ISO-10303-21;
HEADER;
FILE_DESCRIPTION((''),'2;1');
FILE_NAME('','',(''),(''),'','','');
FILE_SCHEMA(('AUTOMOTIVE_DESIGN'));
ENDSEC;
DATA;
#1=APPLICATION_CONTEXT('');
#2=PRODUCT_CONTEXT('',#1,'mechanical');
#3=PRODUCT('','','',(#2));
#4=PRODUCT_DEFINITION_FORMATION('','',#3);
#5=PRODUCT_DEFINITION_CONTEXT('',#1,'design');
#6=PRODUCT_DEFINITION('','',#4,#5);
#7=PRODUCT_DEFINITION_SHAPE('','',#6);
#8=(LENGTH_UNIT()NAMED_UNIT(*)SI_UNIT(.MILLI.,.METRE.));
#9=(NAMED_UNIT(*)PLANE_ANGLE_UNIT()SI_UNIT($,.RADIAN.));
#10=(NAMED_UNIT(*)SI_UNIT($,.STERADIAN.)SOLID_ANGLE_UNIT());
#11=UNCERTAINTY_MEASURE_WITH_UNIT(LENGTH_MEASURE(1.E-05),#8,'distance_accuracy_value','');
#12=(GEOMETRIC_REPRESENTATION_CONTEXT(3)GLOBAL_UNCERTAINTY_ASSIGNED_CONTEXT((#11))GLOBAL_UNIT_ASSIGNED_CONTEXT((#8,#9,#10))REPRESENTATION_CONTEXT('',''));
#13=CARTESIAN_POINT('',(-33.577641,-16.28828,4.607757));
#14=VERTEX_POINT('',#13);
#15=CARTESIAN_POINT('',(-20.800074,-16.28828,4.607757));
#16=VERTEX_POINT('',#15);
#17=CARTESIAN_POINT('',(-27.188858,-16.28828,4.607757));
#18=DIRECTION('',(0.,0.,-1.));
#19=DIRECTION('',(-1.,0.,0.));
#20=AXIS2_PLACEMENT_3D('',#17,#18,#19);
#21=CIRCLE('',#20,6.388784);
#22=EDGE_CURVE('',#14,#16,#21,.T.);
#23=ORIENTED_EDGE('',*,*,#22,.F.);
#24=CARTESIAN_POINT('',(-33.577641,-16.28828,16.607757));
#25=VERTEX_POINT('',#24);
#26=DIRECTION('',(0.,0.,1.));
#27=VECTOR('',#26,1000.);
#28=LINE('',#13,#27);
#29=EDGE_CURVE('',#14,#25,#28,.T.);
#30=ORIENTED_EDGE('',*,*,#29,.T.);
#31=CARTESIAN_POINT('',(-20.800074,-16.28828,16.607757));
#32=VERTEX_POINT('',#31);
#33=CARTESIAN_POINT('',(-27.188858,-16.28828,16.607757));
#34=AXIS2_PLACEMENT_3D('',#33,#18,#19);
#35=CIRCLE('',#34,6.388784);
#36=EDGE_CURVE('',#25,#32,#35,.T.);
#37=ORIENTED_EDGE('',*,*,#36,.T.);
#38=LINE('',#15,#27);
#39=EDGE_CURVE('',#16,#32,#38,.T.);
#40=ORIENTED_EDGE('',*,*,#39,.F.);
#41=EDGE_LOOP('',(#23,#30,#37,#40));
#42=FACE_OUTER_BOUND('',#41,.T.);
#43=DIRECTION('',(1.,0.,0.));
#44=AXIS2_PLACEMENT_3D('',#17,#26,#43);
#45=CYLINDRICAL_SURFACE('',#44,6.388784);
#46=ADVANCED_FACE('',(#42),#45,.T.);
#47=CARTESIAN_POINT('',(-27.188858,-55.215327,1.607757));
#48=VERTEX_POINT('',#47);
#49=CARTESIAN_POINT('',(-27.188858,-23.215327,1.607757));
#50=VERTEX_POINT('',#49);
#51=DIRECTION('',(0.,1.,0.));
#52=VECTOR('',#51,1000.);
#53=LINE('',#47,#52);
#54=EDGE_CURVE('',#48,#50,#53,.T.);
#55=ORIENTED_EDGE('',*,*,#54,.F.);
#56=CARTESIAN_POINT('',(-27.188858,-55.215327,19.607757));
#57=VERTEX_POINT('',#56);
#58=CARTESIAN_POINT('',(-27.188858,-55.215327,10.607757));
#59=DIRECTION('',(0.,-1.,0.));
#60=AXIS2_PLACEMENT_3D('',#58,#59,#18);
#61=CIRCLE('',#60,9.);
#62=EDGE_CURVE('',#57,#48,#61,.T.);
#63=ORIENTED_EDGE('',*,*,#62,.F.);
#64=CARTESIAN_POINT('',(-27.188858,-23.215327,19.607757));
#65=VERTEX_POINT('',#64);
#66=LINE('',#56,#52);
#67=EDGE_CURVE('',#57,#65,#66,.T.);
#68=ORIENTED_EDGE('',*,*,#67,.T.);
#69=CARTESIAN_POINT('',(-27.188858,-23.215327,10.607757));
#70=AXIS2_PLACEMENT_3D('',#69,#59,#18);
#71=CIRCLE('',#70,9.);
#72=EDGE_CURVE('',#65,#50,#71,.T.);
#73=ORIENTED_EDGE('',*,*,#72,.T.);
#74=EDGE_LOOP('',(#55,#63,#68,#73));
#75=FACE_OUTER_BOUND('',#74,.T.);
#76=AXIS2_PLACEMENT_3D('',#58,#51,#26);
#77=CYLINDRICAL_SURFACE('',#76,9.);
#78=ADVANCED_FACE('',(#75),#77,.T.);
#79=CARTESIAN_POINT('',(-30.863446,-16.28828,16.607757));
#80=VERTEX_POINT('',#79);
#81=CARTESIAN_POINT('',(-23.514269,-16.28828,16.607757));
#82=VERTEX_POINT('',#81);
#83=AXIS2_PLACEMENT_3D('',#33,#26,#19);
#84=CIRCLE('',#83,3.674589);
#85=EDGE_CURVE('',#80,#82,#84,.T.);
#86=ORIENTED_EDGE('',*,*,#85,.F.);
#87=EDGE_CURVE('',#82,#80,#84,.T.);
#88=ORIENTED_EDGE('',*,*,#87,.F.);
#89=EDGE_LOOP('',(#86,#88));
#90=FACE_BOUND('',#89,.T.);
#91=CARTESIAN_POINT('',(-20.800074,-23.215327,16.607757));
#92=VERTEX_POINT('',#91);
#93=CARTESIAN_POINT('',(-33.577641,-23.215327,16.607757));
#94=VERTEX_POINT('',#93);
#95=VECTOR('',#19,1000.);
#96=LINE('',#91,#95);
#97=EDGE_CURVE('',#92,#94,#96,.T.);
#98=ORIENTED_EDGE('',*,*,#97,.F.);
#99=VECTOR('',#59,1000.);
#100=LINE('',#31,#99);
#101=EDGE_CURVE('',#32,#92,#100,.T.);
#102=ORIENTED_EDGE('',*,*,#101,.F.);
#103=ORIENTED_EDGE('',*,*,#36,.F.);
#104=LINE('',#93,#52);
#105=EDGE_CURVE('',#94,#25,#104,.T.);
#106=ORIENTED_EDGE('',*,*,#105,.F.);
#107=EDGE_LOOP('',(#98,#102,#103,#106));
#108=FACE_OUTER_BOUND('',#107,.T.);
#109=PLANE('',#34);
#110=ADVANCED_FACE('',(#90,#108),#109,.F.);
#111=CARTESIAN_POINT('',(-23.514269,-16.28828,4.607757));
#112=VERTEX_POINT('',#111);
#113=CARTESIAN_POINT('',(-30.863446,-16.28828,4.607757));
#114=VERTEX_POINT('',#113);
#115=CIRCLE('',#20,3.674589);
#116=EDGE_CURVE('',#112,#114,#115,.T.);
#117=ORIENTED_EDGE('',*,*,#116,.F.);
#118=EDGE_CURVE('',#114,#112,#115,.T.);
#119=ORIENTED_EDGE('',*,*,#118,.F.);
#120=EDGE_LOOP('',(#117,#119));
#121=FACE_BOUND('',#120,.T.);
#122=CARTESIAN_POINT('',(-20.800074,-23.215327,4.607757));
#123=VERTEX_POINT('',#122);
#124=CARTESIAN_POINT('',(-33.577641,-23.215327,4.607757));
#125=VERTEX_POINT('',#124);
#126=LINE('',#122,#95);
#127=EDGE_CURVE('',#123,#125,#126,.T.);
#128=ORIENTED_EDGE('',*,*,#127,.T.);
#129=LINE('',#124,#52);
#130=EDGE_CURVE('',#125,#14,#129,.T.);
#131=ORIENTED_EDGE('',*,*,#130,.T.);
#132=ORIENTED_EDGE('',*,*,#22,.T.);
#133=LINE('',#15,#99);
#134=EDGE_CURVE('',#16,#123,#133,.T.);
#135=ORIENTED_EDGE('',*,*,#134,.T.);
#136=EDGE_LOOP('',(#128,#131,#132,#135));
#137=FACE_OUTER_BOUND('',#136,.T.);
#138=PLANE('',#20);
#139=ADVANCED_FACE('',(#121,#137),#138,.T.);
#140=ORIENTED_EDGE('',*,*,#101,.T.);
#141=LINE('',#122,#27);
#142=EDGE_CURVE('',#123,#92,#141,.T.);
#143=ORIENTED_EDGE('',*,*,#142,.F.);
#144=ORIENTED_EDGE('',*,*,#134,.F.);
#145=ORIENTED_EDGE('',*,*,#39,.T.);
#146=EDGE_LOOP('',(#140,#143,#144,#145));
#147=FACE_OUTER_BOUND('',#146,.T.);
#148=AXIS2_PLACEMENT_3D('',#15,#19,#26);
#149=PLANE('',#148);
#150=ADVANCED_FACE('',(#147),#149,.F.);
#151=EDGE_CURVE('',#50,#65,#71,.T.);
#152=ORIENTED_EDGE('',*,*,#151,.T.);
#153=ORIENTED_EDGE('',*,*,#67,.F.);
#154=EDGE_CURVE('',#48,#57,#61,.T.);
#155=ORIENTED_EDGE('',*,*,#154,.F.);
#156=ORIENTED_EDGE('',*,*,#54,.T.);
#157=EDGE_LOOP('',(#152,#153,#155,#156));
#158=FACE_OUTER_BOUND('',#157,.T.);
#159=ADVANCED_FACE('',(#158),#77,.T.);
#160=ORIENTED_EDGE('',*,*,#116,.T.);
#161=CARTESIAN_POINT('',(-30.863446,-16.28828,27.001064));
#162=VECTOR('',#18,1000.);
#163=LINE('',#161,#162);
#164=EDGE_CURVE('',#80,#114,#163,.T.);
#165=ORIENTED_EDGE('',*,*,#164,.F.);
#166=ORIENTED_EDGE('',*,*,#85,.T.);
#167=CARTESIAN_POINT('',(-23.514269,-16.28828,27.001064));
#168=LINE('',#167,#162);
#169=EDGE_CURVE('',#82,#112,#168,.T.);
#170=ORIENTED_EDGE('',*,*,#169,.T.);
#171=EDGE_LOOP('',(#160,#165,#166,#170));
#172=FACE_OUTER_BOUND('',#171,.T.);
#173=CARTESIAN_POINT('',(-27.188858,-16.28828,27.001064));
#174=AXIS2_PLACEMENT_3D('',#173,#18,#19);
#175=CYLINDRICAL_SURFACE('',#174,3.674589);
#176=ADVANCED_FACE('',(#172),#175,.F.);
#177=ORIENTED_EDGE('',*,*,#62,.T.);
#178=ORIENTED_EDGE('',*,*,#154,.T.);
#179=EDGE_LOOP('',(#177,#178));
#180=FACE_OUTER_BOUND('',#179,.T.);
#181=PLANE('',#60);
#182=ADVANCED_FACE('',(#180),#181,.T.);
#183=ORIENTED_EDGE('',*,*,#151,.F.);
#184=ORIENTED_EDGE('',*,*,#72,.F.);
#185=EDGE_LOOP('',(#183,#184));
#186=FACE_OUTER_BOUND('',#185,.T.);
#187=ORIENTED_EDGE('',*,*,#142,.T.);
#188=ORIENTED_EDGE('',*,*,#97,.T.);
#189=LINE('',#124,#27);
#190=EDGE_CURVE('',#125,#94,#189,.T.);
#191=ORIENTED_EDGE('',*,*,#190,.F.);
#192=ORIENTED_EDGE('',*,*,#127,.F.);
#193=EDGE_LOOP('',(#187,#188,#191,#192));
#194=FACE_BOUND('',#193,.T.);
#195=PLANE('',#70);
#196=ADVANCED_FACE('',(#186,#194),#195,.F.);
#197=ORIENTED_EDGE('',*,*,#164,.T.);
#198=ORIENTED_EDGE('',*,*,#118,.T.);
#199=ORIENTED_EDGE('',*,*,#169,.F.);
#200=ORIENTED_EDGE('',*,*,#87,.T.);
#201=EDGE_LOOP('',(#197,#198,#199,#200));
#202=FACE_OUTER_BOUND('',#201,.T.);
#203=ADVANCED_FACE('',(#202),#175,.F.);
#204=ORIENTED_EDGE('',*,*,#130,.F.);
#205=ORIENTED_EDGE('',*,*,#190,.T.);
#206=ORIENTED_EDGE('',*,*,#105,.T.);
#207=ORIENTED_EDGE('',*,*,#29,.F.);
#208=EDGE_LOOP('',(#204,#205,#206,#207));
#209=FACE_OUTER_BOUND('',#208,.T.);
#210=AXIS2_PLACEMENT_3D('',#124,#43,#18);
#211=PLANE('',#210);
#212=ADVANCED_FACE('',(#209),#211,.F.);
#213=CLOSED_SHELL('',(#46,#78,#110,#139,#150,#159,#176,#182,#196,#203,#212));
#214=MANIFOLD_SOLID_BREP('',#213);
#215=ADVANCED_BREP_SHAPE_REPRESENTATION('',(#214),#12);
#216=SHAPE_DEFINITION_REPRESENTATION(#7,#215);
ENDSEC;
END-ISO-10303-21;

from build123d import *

# Parameters (mm, degrees)
BOSS_EXTRUDE1_DEPTH = 6
SKETCH3_R           = 9
BOSS_EXTRUDE2_DEPTH = 32
SKETCH5_R           = 3.674588618
CUT_EXTRUDE1_DEPTH  = 12


with BuildPart() as part:
    # Sketch2 → Boss-Extrude1 (new, symmetric)
    with BuildSketch(Plane(origin=(0, 0, 10.607757446), x_dir=(-1, 0, 0), z_dir=(0, 0, -1))):
        with BuildLine():
            Line((20.800074125, -16.288280471), (20.800074125, -23.215326818))
            Line((20.800074125, -23.215326818), (33.57764138, -23.215326818))
            Line((33.57764138, -23.215326818), (33.57764138, -16.288280471))
            ThreePointArc((33.57764138, -16.288280471), (27.188857752, -9.899496844), (20.800074125, -16.288280471))
        make_face()
    extrude(amount=BOSS_EXTRUDE1_DEPTH, both=True)

    # Sketch3 → Boss-Extrude2 (add)
    with BuildSketch(Plane.XZ.offset(23.215326818)):
        with Locations(Location((-27.188857752, 10.607757446, 0), (0, 0, 270))):
            Circle(SKETCH3_R)
    extrude(amount=BOSS_EXTRUDE2_DEPTH)

    # Sketch5 → Cut-Extrude1 (cut)
    with BuildSketch(Plane(origin=(0, 0, 4.607757446), x_dir=(-1, 0, 0), z_dir=(0, 0, -1))):
        with Locations((27.188857752, -16.288280471)):
            Circle(SKETCH5_R)
    extrude(amount=-CUT_EXTRUDE1_DEPTH, mode=Mode.SUBTRACT)


solid = part.part
